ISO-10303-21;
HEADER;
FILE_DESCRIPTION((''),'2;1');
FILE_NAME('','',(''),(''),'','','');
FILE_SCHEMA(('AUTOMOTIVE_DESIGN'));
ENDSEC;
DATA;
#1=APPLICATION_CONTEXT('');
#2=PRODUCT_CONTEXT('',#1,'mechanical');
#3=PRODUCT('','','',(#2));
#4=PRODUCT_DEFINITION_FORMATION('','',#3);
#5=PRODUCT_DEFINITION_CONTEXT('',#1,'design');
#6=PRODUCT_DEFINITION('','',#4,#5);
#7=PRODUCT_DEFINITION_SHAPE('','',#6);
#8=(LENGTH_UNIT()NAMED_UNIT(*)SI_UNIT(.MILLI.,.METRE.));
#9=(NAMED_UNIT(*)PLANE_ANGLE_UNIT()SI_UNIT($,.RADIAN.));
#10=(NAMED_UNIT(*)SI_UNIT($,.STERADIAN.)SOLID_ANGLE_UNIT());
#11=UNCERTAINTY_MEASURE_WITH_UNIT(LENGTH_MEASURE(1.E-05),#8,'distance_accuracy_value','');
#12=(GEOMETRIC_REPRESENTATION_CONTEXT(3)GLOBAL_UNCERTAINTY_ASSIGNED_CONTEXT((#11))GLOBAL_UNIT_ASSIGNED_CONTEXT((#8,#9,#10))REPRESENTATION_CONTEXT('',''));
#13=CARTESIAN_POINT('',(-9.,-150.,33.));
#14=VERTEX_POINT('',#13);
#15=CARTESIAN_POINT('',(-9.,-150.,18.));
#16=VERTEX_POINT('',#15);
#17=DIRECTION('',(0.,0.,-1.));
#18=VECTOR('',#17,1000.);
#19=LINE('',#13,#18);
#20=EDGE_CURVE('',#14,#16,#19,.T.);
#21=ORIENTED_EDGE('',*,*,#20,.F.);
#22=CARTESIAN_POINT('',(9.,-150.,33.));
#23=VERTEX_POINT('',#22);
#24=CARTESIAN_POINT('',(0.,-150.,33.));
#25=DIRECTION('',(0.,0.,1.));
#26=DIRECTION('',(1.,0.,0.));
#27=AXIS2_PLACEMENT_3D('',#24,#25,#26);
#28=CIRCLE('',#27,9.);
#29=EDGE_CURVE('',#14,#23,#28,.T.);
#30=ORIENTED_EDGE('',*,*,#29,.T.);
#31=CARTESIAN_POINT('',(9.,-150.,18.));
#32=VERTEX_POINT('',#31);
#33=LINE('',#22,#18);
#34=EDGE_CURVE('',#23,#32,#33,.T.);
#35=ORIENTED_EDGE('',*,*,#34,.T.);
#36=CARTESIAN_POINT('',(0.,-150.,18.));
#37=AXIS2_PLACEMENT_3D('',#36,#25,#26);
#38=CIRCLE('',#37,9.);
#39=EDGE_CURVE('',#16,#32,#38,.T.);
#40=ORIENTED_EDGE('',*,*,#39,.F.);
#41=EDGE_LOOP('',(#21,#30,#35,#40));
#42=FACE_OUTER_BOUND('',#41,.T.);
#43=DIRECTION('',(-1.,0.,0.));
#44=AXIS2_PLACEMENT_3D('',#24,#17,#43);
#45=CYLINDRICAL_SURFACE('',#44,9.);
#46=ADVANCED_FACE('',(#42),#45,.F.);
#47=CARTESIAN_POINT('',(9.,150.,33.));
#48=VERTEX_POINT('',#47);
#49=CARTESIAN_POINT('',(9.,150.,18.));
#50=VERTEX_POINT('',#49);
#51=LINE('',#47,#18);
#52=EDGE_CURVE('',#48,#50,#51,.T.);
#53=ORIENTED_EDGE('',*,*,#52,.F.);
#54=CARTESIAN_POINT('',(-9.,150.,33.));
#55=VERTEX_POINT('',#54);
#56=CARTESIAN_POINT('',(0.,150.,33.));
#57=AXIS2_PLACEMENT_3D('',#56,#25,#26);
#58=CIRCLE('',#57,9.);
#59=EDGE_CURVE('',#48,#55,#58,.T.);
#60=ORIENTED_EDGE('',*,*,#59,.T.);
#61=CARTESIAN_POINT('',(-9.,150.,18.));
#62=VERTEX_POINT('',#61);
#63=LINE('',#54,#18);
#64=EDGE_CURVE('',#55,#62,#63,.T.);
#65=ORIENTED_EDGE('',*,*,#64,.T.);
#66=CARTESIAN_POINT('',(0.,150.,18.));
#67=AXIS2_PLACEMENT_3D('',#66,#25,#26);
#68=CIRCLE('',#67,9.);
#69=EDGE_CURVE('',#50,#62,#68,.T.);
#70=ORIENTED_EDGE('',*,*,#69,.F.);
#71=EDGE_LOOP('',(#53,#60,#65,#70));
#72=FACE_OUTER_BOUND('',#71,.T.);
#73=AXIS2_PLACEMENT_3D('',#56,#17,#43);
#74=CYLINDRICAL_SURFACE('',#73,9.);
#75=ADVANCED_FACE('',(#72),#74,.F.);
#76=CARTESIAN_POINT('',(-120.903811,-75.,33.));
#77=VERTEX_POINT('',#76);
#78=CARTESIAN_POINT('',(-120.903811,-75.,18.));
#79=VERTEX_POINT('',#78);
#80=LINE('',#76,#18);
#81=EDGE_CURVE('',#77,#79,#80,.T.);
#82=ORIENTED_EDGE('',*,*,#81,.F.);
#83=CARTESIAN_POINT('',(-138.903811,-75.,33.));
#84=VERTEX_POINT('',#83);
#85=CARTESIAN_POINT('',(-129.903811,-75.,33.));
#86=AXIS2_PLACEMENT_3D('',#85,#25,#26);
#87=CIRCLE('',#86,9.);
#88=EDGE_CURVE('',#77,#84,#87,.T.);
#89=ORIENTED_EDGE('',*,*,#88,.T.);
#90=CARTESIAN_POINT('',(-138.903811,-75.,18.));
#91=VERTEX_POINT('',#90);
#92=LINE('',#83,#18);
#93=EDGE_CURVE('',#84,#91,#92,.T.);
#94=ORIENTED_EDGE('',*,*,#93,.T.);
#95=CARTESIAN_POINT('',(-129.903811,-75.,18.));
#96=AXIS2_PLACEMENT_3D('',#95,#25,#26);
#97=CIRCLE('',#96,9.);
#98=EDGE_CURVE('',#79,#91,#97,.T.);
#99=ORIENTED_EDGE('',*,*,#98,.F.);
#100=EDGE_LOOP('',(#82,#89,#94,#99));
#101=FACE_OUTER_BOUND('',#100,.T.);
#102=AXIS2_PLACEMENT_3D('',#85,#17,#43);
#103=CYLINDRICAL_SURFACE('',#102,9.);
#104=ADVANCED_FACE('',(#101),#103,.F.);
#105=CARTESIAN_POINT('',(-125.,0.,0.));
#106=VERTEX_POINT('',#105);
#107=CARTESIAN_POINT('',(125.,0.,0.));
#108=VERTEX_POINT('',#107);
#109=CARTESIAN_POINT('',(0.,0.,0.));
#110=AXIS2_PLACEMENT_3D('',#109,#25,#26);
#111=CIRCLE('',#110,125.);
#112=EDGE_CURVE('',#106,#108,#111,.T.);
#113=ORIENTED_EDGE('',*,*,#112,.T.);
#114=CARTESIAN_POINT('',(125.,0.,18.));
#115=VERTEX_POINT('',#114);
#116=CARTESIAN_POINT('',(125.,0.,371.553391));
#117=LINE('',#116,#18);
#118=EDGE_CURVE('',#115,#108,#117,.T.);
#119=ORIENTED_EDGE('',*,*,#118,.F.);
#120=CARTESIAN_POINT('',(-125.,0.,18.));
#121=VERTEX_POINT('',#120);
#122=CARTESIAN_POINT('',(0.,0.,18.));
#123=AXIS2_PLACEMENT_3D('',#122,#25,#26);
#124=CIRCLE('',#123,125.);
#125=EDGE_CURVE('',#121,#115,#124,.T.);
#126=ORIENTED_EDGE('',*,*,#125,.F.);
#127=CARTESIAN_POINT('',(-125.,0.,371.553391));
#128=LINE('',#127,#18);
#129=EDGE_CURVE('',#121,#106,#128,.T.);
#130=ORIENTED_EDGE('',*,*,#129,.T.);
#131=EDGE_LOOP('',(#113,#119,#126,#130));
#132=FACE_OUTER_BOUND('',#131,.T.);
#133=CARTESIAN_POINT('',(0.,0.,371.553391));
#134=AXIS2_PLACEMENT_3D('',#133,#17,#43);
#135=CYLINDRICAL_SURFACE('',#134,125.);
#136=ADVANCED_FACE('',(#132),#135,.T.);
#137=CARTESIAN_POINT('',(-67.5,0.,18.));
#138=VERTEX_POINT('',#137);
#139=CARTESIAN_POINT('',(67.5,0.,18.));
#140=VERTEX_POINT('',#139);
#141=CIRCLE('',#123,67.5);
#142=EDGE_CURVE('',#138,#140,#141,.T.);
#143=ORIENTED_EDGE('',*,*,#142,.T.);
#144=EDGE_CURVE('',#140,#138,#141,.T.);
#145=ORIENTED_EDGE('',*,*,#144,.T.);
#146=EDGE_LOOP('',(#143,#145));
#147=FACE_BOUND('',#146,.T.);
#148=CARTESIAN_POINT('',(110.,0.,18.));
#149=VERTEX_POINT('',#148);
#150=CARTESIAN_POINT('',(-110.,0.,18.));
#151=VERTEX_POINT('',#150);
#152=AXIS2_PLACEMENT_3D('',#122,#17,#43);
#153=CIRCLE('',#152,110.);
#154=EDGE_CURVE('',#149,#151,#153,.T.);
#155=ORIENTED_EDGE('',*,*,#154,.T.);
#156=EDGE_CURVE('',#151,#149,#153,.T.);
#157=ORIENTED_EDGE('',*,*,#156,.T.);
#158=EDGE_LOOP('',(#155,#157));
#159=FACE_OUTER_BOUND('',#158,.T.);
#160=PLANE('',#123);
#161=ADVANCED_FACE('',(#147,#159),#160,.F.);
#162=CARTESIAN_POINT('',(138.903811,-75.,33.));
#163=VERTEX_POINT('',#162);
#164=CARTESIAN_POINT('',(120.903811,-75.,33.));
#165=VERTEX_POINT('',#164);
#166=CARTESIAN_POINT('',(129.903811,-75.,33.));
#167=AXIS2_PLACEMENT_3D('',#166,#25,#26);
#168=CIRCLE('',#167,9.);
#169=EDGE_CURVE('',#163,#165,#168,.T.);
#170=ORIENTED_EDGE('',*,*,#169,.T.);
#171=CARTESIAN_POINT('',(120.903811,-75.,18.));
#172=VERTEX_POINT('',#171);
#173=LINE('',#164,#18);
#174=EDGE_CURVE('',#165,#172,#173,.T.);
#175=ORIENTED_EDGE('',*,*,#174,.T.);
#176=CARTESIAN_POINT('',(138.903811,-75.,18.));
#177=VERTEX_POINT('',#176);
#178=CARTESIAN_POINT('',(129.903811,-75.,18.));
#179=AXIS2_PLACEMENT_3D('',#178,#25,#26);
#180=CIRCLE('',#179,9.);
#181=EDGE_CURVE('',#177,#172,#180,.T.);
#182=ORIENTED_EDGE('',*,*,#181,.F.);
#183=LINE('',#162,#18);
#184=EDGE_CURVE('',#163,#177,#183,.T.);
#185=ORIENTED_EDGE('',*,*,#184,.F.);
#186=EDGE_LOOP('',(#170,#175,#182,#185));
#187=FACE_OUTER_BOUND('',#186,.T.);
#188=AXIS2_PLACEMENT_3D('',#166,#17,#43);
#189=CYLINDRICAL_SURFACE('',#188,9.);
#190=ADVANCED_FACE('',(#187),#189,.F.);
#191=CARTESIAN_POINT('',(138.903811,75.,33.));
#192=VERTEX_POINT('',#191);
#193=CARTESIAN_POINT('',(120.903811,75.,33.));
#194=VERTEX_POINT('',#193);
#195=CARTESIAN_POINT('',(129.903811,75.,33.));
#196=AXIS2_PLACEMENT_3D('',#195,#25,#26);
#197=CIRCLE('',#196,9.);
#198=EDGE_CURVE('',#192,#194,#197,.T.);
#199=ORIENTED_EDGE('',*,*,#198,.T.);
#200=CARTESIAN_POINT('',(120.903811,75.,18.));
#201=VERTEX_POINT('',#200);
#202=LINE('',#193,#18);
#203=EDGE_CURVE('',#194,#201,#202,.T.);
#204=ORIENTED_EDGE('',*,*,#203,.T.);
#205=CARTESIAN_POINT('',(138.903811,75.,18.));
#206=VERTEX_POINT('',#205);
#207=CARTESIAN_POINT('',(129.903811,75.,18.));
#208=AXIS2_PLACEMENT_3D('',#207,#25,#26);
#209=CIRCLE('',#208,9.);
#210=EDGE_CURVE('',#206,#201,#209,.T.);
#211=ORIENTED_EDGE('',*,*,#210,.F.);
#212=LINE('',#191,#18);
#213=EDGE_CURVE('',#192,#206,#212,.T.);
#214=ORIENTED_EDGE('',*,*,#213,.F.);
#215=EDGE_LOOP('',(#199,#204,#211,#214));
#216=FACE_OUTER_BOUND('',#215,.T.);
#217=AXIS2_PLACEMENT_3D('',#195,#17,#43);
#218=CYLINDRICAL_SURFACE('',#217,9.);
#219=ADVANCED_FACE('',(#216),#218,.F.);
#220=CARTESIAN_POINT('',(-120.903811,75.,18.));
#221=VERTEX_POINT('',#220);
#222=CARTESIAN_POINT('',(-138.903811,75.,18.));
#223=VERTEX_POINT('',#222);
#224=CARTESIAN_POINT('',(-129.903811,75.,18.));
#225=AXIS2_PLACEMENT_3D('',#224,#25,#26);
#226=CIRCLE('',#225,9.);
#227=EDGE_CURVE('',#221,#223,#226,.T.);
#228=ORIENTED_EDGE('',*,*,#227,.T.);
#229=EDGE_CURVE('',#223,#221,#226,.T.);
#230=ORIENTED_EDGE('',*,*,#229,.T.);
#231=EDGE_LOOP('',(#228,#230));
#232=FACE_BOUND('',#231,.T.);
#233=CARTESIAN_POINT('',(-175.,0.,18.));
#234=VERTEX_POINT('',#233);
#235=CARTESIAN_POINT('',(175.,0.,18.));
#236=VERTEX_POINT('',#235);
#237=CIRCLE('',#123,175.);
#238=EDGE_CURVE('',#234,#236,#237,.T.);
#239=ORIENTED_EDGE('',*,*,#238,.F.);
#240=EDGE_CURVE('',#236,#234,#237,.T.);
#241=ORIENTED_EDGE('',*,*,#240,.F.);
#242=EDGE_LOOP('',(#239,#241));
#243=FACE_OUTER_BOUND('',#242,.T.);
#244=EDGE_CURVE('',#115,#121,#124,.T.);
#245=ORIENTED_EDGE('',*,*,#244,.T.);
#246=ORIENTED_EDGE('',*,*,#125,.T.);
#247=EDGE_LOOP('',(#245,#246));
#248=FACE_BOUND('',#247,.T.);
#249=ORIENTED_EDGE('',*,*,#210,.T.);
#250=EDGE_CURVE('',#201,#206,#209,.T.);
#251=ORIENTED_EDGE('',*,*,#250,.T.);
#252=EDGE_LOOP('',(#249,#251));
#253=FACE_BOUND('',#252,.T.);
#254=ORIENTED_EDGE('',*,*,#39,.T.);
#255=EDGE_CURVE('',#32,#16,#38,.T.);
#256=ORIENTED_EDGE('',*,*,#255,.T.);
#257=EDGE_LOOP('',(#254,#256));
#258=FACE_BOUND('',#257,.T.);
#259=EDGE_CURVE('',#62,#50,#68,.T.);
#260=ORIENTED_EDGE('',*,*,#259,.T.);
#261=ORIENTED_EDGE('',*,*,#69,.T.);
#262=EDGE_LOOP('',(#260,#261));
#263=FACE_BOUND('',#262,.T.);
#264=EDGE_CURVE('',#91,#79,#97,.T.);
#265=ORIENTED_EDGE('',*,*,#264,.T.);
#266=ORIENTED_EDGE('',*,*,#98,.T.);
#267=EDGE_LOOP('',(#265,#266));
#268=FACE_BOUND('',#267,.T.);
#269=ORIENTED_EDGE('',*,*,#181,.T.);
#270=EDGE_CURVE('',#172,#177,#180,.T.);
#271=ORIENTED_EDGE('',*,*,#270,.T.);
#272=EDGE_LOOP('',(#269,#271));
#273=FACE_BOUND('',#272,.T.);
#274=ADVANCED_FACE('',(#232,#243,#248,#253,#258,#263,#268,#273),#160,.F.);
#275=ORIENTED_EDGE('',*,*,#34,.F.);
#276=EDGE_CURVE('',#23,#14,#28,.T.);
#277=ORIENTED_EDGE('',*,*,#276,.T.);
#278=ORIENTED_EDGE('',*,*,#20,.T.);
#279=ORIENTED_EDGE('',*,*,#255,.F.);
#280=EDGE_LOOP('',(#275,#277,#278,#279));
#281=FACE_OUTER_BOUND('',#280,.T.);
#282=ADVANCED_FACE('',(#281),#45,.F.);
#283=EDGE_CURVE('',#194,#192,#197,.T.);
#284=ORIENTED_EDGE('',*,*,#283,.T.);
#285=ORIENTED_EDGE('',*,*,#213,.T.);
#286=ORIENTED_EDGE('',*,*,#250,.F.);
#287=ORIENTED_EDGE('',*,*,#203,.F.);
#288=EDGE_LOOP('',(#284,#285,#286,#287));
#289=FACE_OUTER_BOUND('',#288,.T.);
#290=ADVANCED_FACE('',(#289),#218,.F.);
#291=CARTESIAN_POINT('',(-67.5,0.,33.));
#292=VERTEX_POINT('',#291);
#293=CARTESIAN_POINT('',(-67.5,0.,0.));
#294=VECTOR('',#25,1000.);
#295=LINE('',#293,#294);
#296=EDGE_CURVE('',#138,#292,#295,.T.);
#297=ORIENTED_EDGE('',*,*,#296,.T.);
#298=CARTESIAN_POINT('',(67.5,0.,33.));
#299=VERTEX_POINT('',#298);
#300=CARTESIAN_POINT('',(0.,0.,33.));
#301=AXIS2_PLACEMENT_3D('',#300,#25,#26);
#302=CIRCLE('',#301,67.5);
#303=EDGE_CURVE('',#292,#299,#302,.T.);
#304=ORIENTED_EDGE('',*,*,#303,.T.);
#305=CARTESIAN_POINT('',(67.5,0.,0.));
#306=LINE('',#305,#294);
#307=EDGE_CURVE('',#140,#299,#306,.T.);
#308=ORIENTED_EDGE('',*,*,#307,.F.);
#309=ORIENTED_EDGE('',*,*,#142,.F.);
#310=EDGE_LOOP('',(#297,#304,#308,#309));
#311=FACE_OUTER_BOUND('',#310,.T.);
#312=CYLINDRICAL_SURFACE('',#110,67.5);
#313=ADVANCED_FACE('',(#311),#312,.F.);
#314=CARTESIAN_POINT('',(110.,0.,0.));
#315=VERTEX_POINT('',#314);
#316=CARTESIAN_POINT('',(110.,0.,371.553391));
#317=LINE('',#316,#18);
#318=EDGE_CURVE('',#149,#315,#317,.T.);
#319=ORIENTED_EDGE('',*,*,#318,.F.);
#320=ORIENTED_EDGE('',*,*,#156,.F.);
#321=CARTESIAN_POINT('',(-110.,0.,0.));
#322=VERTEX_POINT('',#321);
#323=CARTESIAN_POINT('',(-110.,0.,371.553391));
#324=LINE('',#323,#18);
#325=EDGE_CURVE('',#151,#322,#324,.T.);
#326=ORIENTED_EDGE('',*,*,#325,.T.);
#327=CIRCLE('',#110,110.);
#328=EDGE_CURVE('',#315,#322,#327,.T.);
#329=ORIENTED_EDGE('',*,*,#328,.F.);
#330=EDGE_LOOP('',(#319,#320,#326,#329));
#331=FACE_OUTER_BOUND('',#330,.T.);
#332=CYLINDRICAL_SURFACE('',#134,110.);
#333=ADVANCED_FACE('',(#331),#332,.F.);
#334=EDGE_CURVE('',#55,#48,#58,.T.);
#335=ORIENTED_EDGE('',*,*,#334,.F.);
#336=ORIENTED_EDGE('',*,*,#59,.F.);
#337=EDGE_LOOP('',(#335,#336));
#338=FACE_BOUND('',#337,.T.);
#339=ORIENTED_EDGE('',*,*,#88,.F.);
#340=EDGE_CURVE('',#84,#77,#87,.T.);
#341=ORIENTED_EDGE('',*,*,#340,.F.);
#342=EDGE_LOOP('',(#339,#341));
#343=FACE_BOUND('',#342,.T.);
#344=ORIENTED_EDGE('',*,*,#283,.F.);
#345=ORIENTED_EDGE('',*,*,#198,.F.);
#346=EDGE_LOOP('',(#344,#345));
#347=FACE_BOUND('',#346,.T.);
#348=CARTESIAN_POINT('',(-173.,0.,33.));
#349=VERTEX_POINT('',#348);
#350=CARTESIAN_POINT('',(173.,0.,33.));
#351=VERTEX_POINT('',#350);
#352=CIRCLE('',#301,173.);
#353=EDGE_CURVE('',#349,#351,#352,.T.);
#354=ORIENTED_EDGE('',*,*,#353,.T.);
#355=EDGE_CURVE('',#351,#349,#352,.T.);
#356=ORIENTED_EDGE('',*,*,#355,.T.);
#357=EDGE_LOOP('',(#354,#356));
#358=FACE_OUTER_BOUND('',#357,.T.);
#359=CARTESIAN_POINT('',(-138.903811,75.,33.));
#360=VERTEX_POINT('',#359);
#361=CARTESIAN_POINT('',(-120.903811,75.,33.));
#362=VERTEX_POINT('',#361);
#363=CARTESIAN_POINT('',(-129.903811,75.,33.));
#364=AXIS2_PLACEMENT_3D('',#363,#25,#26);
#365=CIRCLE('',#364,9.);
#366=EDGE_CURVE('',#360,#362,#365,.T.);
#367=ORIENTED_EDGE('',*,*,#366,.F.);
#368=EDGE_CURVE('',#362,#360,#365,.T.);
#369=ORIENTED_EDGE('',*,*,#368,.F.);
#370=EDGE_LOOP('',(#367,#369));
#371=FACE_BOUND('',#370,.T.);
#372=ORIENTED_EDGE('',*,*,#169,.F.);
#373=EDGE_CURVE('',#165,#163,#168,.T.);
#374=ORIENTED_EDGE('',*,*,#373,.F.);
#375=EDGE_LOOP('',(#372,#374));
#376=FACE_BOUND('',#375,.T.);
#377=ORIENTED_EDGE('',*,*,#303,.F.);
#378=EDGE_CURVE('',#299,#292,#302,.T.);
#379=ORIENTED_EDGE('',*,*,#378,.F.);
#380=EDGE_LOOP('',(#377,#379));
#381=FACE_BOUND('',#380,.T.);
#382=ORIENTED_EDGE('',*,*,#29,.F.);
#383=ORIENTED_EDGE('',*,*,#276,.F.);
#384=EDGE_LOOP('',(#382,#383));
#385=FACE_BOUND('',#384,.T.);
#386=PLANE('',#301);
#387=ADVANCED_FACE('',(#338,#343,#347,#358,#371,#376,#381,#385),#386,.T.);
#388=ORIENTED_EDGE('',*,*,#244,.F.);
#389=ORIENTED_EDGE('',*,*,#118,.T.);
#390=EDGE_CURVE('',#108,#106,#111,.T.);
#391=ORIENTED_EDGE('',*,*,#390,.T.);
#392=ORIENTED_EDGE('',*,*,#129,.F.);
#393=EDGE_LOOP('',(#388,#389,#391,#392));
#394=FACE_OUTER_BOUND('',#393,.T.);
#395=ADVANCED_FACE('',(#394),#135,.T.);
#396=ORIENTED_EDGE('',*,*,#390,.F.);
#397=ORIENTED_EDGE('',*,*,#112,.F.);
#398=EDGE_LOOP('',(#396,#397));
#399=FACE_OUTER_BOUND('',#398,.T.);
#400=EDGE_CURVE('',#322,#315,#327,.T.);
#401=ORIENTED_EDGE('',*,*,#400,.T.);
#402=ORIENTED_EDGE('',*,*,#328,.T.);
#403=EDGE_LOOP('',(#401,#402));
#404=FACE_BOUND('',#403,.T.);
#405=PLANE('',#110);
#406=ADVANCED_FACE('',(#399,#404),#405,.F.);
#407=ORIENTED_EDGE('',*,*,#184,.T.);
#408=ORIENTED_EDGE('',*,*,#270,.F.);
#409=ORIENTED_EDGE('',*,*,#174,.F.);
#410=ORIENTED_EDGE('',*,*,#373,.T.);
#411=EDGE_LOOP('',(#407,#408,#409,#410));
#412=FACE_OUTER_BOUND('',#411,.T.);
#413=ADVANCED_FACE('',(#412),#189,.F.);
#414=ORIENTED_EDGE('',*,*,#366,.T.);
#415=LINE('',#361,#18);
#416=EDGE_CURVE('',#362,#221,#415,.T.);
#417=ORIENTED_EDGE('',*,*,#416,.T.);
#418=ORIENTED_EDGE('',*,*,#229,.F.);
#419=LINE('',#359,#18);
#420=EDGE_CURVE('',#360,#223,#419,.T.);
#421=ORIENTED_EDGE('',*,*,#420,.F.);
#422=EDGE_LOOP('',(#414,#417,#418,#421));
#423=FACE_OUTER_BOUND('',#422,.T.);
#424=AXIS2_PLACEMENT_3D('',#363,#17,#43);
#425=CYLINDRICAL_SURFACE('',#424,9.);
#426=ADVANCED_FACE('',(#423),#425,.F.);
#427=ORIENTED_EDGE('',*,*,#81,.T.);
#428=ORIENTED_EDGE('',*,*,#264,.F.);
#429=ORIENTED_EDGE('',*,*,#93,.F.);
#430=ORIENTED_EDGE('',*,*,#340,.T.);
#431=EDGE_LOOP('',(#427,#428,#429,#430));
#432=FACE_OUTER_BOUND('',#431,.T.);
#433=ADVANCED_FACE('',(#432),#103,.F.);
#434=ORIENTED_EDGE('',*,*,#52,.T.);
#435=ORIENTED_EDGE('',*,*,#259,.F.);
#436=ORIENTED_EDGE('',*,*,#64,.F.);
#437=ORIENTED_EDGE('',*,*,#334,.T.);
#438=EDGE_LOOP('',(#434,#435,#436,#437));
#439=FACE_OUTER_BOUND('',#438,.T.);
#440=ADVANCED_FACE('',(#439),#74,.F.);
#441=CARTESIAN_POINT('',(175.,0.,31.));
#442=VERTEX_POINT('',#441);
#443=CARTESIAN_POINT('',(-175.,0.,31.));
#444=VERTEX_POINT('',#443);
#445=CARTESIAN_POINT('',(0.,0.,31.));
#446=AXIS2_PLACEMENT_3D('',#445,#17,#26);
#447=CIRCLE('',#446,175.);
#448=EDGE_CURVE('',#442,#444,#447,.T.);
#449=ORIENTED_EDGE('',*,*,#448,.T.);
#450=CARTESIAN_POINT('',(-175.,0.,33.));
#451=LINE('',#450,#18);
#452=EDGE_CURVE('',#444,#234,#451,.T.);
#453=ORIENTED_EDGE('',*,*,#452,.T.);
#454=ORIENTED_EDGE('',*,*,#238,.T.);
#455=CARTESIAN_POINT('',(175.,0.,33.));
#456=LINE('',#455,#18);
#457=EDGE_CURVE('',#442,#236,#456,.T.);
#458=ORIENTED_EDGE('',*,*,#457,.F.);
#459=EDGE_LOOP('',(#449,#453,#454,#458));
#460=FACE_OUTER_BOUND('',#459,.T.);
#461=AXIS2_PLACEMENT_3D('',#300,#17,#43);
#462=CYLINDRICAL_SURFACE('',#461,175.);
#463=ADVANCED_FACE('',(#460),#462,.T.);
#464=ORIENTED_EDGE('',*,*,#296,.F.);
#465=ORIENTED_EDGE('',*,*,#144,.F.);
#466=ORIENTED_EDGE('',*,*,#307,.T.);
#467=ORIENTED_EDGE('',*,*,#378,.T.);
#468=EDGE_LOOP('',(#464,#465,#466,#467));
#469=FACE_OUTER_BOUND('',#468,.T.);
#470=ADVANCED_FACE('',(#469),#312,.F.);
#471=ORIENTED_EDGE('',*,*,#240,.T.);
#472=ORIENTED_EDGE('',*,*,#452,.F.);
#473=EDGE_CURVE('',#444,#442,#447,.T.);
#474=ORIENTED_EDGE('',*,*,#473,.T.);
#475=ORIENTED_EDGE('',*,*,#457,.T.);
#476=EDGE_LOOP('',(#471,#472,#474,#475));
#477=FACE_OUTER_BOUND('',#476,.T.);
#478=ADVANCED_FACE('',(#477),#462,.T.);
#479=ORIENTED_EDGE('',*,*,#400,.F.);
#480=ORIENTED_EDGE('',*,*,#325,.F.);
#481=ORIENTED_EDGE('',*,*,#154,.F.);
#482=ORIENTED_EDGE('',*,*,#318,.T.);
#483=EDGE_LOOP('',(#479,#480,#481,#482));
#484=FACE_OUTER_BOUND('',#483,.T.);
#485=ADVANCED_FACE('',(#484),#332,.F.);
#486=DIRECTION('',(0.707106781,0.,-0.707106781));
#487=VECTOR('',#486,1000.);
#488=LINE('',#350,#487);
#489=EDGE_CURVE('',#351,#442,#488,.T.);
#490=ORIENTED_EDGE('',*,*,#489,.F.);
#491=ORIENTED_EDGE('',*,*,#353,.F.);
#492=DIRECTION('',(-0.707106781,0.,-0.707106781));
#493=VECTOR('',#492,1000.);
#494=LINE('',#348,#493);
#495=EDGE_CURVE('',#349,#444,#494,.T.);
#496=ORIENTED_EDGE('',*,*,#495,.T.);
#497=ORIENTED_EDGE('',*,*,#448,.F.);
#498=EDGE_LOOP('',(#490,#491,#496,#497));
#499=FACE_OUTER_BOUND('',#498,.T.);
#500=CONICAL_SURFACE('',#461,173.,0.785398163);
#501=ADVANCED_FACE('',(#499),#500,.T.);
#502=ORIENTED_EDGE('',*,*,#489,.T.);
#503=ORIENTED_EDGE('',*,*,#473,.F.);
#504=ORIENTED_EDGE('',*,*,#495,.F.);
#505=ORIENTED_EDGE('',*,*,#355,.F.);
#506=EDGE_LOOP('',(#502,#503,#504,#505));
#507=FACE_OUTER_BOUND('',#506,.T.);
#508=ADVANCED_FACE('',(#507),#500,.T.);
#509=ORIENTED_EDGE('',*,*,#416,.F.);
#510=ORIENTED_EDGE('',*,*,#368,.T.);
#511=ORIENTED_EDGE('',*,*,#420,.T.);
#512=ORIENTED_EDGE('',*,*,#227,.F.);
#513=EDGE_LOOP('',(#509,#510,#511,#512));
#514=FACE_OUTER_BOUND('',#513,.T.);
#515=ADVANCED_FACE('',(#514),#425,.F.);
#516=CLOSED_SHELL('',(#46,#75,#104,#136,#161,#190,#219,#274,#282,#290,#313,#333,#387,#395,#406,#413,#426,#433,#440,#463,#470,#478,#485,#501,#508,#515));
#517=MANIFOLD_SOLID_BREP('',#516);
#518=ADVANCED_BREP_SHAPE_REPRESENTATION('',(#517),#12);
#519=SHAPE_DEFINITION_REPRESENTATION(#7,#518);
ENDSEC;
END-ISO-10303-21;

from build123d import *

# Parameters (mm, degrees)
SKETCH1_R           = 125
SKETCH1_R_2         = 110
BOSS_EXTRUDE1_DEPTH = 18
SKETCH2_R           = 175
SKETCH2_R_2         = 9
BOSS_EXTRUDE2_DEPTH = 15
CHAMFER1_SIZE       = 2
SKETCH3_R           = 67.5
CUT_EXTRUDE1_DEPTH  = 250.677792364


with BuildPart() as part:
    # Sketch1 → Boss-Extrude1 (new body)
    with BuildSketch(Plane.XY):
        with Locations(Location((0, 0, 0), (0, 0, 180))):
            Circle(SKETCH1_R)
        with Locations(Location((0, 0, 0), (0, 0, 180))):
            Circle(SKETCH1_R_2, mode=Mode.SUBTRACT)
    extrude(amount=BOSS_EXTRUDE1_DEPTH)

    # Sketch2 → Boss-Extrude2 (add)
    with BuildSketch(Plane.XY.offset(18)):
        Circle(SKETCH2_R)
        with Locations((0, 150)):
            Circle(SKETCH2_R_2, mode=Mode.SUBTRACT)
        with Locations((-129.903810568, 75)):
            Circle(SKETCH2_R_2, mode=Mode.SUBTRACT)
        with Locations((-129.903810568, -75)):
            Circle(SKETCH2_R_2, mode=Mode.SUBTRACT)
        with Locations((0, -150)):
            Circle(SKETCH2_R_2, mode=Mode.SUBTRACT)
        with Locations((129.903810568, -75)):
            Circle(SKETCH2_R_2, mode=Mode.SUBTRACT)
        with Locations((129.903810568, 75)):
            Circle(SKETCH2_R_2, mode=Mode.SUBTRACT)
    extrude(amount=BOSS_EXTRUDE2_DEPTH)

    # Chamfer1
    chamfer1_edges = [part.edges().sort_by_distance(p)[0] for p in [
        (-175, 0, 33),
    ]]
    chamfer(chamfer1_edges, length=CHAMFER1_SIZE)

    # Sketch3 → Cut-Extrude1 (cut, through all)
    with BuildSketch(Plane.XY.offset(33)):
        Circle(SKETCH3_R)
    extrude(amount=-CUT_EXTRUDE1_DEPTH, mode=Mode.SUBTRACT)


solid = part.part
